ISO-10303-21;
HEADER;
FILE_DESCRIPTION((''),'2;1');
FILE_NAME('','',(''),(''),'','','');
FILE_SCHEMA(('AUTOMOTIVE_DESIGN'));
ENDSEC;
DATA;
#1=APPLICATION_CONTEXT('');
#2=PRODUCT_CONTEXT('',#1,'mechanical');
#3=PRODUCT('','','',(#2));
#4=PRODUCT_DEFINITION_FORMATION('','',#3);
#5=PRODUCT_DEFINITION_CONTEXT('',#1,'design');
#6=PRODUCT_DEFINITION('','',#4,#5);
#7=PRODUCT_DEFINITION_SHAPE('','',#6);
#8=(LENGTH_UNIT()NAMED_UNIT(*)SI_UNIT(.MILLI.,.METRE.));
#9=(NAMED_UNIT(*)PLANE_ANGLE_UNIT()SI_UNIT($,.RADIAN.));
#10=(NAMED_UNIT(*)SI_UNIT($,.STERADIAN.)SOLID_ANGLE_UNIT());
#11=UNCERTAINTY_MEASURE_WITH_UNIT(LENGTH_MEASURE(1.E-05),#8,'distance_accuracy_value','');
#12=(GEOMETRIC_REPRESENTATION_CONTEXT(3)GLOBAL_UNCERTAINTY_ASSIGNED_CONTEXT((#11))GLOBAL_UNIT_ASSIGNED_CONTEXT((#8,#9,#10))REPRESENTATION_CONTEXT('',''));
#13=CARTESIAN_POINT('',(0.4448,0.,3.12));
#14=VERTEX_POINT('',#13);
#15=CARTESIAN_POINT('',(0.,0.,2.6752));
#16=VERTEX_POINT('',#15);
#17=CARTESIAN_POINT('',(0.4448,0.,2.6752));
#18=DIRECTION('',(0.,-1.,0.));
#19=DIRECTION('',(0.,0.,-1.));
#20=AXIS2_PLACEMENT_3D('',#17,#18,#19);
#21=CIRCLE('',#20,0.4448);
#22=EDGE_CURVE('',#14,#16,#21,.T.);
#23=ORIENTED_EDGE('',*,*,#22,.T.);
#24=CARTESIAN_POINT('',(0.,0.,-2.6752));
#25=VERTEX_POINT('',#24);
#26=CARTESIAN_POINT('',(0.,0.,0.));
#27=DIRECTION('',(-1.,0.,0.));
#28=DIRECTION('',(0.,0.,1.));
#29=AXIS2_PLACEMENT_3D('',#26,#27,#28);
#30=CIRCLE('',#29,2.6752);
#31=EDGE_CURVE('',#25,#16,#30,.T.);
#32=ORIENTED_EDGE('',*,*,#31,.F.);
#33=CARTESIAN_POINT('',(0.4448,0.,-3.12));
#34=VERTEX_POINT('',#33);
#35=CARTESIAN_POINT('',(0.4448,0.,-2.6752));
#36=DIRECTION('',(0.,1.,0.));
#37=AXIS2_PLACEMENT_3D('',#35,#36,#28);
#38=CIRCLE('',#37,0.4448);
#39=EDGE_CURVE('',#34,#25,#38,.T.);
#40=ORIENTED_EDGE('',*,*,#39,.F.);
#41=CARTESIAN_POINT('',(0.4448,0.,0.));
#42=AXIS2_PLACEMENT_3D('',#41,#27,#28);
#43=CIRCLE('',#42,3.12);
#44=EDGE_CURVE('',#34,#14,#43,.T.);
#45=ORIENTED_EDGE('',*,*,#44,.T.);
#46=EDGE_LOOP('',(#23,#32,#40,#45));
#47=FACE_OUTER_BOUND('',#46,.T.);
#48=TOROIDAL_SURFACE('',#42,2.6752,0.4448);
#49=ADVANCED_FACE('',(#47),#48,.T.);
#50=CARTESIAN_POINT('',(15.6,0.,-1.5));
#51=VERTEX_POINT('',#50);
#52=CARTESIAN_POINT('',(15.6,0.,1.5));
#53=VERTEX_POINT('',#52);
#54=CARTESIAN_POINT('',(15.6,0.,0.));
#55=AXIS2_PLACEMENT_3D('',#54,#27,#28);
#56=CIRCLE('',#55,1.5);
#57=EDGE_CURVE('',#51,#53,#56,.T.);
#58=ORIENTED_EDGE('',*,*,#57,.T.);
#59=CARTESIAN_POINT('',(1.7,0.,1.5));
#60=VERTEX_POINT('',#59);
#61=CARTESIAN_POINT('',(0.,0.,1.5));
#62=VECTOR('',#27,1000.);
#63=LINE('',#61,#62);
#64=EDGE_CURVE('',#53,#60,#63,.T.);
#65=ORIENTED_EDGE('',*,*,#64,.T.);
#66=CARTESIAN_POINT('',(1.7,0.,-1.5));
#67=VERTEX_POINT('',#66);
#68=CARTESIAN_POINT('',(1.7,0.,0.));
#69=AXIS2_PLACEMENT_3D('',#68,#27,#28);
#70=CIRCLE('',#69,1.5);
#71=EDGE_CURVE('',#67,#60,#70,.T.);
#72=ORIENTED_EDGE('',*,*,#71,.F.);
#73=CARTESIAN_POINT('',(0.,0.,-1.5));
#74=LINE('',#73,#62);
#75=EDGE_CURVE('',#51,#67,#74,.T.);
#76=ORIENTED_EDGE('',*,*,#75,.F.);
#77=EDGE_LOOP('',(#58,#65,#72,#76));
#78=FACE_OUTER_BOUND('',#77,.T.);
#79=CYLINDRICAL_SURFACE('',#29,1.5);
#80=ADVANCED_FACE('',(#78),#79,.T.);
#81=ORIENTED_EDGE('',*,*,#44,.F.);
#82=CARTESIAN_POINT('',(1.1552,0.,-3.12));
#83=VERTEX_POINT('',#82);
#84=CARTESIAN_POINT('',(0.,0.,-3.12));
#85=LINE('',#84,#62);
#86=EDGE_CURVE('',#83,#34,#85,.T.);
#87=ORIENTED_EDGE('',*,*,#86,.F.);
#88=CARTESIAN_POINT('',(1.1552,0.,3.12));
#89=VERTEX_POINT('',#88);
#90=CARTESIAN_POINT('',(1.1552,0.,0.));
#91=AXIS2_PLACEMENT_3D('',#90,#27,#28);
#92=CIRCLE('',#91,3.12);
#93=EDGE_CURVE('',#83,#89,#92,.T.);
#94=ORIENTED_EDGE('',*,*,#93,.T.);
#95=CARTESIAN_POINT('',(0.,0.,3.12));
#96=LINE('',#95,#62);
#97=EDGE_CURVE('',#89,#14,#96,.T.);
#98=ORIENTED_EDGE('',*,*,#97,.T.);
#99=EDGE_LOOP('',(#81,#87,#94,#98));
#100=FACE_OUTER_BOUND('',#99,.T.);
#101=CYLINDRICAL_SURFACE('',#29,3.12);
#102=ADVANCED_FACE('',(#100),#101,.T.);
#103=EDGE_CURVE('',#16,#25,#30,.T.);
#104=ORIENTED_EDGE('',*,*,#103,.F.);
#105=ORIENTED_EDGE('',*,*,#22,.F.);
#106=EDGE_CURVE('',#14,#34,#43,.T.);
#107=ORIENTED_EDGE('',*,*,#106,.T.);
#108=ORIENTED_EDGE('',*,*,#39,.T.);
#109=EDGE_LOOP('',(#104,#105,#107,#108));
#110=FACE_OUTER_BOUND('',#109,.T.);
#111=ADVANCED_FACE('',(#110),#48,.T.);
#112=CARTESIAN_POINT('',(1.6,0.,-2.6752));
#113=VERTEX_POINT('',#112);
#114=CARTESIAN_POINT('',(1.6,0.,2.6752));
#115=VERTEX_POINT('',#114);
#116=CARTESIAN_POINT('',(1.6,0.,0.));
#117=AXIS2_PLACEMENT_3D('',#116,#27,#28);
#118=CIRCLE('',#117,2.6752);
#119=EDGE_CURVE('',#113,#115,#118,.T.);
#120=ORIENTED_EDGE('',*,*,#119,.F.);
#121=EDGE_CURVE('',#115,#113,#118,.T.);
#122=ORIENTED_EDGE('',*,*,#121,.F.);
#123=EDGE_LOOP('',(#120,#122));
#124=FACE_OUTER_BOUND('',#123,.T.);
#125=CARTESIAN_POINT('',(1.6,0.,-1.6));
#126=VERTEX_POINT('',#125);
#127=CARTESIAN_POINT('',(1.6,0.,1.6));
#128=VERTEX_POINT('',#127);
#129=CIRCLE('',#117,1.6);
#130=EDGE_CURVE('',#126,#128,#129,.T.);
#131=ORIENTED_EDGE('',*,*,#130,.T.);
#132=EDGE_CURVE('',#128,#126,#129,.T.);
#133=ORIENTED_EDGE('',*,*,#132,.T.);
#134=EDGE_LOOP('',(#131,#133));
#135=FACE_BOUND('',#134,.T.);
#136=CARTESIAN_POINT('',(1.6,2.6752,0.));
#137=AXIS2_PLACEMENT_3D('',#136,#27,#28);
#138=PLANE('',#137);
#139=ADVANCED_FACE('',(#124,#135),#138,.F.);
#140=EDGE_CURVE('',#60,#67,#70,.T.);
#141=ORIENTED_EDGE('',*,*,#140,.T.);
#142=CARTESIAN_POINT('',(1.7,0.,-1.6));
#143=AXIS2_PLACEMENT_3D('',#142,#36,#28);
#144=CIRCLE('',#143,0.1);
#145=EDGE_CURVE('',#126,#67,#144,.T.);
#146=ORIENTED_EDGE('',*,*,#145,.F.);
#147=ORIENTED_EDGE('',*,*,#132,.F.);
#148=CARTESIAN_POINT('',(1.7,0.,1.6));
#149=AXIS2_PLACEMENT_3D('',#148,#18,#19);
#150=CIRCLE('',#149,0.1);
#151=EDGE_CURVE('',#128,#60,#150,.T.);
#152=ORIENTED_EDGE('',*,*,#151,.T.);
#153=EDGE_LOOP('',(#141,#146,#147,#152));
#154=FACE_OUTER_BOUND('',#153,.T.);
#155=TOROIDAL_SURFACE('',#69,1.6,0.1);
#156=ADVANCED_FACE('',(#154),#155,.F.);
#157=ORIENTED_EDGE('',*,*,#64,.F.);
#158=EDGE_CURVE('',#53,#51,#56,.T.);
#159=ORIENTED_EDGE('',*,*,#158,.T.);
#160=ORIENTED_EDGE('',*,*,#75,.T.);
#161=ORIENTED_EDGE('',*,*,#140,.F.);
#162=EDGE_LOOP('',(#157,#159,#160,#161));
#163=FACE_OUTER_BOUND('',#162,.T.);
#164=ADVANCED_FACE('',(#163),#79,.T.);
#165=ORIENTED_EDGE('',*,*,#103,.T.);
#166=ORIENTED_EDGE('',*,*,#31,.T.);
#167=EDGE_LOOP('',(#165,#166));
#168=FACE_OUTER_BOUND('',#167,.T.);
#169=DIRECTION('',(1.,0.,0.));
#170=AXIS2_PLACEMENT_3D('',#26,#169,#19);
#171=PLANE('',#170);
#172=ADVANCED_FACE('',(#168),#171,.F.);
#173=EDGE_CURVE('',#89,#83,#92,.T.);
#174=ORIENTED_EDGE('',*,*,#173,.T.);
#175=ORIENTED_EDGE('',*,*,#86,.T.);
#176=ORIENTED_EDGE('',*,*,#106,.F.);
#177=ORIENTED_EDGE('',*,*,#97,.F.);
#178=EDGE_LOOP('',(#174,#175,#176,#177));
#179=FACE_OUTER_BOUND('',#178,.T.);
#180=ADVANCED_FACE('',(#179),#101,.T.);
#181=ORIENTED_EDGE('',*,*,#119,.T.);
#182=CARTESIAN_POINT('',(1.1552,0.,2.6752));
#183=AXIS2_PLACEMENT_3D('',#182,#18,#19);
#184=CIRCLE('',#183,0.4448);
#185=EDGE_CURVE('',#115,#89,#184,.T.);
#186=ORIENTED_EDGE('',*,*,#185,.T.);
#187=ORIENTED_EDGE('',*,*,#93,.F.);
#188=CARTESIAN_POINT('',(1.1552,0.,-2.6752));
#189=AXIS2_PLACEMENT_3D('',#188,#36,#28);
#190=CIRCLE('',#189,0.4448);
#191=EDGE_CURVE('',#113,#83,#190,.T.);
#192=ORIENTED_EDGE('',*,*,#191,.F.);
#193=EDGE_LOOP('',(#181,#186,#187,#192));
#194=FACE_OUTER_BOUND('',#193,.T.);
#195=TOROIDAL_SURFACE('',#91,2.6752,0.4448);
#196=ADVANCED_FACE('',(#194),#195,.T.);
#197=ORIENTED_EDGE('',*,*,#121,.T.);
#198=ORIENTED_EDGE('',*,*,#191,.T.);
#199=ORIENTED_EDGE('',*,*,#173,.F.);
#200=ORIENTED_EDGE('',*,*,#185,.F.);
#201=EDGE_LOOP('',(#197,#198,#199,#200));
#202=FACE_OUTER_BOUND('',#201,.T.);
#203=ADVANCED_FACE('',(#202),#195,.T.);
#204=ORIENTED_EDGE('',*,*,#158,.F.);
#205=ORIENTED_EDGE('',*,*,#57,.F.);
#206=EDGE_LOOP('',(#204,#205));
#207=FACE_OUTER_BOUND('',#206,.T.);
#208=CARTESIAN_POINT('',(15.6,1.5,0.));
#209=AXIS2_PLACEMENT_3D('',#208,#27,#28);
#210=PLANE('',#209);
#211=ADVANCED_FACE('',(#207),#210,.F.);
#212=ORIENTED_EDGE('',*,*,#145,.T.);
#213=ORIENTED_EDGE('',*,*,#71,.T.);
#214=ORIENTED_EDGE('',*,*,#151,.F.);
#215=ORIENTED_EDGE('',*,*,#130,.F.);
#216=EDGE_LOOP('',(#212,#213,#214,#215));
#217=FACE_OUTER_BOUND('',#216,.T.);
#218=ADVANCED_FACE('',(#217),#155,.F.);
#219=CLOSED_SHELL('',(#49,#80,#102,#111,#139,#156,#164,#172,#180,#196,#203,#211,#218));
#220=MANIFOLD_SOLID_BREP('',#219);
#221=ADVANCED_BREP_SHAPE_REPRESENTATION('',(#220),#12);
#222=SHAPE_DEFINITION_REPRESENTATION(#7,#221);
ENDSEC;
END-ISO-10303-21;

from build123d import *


with BuildPart() as part:
    # Dimensioned Sketch → Revolve3 (revolve)
    with BuildSketch(Plane.XY, mode=Mode.PRIVATE) as revolve3_sk:
        with BuildLine():
            Line((0, 0), (0, 2.6752))
            ThreePointArc((0, 2.6752), (0.130278904, 2.989721096), (0.4448, 3.12))
            Line((0.4448, 3.12), (1.1552, 3.12))
            ThreePointArc((1.1552, 3.12), (1.469721096, 2.989721096), (1.6, 2.6752))
            Line((1.6, 2.6752), (1.6, 1.6))
            ThreePointArc((1.6, 1.6), (1.629289322, 1.529289322), (1.7, 1.5))
            Line((1.7, 1.5), (15.6, 1.5))
            Line((15.6, 1.5), (15.6, 0))
            Line((15.6, 0), (0, 0))
        make_face()
    revolve(revolve3_sk.sketch.rotate(Axis((0, 0, 0), (1, 0, 0)), 90), axis=Axis((0, 0, 0), (1, 0, 0)))


solid = part.part
